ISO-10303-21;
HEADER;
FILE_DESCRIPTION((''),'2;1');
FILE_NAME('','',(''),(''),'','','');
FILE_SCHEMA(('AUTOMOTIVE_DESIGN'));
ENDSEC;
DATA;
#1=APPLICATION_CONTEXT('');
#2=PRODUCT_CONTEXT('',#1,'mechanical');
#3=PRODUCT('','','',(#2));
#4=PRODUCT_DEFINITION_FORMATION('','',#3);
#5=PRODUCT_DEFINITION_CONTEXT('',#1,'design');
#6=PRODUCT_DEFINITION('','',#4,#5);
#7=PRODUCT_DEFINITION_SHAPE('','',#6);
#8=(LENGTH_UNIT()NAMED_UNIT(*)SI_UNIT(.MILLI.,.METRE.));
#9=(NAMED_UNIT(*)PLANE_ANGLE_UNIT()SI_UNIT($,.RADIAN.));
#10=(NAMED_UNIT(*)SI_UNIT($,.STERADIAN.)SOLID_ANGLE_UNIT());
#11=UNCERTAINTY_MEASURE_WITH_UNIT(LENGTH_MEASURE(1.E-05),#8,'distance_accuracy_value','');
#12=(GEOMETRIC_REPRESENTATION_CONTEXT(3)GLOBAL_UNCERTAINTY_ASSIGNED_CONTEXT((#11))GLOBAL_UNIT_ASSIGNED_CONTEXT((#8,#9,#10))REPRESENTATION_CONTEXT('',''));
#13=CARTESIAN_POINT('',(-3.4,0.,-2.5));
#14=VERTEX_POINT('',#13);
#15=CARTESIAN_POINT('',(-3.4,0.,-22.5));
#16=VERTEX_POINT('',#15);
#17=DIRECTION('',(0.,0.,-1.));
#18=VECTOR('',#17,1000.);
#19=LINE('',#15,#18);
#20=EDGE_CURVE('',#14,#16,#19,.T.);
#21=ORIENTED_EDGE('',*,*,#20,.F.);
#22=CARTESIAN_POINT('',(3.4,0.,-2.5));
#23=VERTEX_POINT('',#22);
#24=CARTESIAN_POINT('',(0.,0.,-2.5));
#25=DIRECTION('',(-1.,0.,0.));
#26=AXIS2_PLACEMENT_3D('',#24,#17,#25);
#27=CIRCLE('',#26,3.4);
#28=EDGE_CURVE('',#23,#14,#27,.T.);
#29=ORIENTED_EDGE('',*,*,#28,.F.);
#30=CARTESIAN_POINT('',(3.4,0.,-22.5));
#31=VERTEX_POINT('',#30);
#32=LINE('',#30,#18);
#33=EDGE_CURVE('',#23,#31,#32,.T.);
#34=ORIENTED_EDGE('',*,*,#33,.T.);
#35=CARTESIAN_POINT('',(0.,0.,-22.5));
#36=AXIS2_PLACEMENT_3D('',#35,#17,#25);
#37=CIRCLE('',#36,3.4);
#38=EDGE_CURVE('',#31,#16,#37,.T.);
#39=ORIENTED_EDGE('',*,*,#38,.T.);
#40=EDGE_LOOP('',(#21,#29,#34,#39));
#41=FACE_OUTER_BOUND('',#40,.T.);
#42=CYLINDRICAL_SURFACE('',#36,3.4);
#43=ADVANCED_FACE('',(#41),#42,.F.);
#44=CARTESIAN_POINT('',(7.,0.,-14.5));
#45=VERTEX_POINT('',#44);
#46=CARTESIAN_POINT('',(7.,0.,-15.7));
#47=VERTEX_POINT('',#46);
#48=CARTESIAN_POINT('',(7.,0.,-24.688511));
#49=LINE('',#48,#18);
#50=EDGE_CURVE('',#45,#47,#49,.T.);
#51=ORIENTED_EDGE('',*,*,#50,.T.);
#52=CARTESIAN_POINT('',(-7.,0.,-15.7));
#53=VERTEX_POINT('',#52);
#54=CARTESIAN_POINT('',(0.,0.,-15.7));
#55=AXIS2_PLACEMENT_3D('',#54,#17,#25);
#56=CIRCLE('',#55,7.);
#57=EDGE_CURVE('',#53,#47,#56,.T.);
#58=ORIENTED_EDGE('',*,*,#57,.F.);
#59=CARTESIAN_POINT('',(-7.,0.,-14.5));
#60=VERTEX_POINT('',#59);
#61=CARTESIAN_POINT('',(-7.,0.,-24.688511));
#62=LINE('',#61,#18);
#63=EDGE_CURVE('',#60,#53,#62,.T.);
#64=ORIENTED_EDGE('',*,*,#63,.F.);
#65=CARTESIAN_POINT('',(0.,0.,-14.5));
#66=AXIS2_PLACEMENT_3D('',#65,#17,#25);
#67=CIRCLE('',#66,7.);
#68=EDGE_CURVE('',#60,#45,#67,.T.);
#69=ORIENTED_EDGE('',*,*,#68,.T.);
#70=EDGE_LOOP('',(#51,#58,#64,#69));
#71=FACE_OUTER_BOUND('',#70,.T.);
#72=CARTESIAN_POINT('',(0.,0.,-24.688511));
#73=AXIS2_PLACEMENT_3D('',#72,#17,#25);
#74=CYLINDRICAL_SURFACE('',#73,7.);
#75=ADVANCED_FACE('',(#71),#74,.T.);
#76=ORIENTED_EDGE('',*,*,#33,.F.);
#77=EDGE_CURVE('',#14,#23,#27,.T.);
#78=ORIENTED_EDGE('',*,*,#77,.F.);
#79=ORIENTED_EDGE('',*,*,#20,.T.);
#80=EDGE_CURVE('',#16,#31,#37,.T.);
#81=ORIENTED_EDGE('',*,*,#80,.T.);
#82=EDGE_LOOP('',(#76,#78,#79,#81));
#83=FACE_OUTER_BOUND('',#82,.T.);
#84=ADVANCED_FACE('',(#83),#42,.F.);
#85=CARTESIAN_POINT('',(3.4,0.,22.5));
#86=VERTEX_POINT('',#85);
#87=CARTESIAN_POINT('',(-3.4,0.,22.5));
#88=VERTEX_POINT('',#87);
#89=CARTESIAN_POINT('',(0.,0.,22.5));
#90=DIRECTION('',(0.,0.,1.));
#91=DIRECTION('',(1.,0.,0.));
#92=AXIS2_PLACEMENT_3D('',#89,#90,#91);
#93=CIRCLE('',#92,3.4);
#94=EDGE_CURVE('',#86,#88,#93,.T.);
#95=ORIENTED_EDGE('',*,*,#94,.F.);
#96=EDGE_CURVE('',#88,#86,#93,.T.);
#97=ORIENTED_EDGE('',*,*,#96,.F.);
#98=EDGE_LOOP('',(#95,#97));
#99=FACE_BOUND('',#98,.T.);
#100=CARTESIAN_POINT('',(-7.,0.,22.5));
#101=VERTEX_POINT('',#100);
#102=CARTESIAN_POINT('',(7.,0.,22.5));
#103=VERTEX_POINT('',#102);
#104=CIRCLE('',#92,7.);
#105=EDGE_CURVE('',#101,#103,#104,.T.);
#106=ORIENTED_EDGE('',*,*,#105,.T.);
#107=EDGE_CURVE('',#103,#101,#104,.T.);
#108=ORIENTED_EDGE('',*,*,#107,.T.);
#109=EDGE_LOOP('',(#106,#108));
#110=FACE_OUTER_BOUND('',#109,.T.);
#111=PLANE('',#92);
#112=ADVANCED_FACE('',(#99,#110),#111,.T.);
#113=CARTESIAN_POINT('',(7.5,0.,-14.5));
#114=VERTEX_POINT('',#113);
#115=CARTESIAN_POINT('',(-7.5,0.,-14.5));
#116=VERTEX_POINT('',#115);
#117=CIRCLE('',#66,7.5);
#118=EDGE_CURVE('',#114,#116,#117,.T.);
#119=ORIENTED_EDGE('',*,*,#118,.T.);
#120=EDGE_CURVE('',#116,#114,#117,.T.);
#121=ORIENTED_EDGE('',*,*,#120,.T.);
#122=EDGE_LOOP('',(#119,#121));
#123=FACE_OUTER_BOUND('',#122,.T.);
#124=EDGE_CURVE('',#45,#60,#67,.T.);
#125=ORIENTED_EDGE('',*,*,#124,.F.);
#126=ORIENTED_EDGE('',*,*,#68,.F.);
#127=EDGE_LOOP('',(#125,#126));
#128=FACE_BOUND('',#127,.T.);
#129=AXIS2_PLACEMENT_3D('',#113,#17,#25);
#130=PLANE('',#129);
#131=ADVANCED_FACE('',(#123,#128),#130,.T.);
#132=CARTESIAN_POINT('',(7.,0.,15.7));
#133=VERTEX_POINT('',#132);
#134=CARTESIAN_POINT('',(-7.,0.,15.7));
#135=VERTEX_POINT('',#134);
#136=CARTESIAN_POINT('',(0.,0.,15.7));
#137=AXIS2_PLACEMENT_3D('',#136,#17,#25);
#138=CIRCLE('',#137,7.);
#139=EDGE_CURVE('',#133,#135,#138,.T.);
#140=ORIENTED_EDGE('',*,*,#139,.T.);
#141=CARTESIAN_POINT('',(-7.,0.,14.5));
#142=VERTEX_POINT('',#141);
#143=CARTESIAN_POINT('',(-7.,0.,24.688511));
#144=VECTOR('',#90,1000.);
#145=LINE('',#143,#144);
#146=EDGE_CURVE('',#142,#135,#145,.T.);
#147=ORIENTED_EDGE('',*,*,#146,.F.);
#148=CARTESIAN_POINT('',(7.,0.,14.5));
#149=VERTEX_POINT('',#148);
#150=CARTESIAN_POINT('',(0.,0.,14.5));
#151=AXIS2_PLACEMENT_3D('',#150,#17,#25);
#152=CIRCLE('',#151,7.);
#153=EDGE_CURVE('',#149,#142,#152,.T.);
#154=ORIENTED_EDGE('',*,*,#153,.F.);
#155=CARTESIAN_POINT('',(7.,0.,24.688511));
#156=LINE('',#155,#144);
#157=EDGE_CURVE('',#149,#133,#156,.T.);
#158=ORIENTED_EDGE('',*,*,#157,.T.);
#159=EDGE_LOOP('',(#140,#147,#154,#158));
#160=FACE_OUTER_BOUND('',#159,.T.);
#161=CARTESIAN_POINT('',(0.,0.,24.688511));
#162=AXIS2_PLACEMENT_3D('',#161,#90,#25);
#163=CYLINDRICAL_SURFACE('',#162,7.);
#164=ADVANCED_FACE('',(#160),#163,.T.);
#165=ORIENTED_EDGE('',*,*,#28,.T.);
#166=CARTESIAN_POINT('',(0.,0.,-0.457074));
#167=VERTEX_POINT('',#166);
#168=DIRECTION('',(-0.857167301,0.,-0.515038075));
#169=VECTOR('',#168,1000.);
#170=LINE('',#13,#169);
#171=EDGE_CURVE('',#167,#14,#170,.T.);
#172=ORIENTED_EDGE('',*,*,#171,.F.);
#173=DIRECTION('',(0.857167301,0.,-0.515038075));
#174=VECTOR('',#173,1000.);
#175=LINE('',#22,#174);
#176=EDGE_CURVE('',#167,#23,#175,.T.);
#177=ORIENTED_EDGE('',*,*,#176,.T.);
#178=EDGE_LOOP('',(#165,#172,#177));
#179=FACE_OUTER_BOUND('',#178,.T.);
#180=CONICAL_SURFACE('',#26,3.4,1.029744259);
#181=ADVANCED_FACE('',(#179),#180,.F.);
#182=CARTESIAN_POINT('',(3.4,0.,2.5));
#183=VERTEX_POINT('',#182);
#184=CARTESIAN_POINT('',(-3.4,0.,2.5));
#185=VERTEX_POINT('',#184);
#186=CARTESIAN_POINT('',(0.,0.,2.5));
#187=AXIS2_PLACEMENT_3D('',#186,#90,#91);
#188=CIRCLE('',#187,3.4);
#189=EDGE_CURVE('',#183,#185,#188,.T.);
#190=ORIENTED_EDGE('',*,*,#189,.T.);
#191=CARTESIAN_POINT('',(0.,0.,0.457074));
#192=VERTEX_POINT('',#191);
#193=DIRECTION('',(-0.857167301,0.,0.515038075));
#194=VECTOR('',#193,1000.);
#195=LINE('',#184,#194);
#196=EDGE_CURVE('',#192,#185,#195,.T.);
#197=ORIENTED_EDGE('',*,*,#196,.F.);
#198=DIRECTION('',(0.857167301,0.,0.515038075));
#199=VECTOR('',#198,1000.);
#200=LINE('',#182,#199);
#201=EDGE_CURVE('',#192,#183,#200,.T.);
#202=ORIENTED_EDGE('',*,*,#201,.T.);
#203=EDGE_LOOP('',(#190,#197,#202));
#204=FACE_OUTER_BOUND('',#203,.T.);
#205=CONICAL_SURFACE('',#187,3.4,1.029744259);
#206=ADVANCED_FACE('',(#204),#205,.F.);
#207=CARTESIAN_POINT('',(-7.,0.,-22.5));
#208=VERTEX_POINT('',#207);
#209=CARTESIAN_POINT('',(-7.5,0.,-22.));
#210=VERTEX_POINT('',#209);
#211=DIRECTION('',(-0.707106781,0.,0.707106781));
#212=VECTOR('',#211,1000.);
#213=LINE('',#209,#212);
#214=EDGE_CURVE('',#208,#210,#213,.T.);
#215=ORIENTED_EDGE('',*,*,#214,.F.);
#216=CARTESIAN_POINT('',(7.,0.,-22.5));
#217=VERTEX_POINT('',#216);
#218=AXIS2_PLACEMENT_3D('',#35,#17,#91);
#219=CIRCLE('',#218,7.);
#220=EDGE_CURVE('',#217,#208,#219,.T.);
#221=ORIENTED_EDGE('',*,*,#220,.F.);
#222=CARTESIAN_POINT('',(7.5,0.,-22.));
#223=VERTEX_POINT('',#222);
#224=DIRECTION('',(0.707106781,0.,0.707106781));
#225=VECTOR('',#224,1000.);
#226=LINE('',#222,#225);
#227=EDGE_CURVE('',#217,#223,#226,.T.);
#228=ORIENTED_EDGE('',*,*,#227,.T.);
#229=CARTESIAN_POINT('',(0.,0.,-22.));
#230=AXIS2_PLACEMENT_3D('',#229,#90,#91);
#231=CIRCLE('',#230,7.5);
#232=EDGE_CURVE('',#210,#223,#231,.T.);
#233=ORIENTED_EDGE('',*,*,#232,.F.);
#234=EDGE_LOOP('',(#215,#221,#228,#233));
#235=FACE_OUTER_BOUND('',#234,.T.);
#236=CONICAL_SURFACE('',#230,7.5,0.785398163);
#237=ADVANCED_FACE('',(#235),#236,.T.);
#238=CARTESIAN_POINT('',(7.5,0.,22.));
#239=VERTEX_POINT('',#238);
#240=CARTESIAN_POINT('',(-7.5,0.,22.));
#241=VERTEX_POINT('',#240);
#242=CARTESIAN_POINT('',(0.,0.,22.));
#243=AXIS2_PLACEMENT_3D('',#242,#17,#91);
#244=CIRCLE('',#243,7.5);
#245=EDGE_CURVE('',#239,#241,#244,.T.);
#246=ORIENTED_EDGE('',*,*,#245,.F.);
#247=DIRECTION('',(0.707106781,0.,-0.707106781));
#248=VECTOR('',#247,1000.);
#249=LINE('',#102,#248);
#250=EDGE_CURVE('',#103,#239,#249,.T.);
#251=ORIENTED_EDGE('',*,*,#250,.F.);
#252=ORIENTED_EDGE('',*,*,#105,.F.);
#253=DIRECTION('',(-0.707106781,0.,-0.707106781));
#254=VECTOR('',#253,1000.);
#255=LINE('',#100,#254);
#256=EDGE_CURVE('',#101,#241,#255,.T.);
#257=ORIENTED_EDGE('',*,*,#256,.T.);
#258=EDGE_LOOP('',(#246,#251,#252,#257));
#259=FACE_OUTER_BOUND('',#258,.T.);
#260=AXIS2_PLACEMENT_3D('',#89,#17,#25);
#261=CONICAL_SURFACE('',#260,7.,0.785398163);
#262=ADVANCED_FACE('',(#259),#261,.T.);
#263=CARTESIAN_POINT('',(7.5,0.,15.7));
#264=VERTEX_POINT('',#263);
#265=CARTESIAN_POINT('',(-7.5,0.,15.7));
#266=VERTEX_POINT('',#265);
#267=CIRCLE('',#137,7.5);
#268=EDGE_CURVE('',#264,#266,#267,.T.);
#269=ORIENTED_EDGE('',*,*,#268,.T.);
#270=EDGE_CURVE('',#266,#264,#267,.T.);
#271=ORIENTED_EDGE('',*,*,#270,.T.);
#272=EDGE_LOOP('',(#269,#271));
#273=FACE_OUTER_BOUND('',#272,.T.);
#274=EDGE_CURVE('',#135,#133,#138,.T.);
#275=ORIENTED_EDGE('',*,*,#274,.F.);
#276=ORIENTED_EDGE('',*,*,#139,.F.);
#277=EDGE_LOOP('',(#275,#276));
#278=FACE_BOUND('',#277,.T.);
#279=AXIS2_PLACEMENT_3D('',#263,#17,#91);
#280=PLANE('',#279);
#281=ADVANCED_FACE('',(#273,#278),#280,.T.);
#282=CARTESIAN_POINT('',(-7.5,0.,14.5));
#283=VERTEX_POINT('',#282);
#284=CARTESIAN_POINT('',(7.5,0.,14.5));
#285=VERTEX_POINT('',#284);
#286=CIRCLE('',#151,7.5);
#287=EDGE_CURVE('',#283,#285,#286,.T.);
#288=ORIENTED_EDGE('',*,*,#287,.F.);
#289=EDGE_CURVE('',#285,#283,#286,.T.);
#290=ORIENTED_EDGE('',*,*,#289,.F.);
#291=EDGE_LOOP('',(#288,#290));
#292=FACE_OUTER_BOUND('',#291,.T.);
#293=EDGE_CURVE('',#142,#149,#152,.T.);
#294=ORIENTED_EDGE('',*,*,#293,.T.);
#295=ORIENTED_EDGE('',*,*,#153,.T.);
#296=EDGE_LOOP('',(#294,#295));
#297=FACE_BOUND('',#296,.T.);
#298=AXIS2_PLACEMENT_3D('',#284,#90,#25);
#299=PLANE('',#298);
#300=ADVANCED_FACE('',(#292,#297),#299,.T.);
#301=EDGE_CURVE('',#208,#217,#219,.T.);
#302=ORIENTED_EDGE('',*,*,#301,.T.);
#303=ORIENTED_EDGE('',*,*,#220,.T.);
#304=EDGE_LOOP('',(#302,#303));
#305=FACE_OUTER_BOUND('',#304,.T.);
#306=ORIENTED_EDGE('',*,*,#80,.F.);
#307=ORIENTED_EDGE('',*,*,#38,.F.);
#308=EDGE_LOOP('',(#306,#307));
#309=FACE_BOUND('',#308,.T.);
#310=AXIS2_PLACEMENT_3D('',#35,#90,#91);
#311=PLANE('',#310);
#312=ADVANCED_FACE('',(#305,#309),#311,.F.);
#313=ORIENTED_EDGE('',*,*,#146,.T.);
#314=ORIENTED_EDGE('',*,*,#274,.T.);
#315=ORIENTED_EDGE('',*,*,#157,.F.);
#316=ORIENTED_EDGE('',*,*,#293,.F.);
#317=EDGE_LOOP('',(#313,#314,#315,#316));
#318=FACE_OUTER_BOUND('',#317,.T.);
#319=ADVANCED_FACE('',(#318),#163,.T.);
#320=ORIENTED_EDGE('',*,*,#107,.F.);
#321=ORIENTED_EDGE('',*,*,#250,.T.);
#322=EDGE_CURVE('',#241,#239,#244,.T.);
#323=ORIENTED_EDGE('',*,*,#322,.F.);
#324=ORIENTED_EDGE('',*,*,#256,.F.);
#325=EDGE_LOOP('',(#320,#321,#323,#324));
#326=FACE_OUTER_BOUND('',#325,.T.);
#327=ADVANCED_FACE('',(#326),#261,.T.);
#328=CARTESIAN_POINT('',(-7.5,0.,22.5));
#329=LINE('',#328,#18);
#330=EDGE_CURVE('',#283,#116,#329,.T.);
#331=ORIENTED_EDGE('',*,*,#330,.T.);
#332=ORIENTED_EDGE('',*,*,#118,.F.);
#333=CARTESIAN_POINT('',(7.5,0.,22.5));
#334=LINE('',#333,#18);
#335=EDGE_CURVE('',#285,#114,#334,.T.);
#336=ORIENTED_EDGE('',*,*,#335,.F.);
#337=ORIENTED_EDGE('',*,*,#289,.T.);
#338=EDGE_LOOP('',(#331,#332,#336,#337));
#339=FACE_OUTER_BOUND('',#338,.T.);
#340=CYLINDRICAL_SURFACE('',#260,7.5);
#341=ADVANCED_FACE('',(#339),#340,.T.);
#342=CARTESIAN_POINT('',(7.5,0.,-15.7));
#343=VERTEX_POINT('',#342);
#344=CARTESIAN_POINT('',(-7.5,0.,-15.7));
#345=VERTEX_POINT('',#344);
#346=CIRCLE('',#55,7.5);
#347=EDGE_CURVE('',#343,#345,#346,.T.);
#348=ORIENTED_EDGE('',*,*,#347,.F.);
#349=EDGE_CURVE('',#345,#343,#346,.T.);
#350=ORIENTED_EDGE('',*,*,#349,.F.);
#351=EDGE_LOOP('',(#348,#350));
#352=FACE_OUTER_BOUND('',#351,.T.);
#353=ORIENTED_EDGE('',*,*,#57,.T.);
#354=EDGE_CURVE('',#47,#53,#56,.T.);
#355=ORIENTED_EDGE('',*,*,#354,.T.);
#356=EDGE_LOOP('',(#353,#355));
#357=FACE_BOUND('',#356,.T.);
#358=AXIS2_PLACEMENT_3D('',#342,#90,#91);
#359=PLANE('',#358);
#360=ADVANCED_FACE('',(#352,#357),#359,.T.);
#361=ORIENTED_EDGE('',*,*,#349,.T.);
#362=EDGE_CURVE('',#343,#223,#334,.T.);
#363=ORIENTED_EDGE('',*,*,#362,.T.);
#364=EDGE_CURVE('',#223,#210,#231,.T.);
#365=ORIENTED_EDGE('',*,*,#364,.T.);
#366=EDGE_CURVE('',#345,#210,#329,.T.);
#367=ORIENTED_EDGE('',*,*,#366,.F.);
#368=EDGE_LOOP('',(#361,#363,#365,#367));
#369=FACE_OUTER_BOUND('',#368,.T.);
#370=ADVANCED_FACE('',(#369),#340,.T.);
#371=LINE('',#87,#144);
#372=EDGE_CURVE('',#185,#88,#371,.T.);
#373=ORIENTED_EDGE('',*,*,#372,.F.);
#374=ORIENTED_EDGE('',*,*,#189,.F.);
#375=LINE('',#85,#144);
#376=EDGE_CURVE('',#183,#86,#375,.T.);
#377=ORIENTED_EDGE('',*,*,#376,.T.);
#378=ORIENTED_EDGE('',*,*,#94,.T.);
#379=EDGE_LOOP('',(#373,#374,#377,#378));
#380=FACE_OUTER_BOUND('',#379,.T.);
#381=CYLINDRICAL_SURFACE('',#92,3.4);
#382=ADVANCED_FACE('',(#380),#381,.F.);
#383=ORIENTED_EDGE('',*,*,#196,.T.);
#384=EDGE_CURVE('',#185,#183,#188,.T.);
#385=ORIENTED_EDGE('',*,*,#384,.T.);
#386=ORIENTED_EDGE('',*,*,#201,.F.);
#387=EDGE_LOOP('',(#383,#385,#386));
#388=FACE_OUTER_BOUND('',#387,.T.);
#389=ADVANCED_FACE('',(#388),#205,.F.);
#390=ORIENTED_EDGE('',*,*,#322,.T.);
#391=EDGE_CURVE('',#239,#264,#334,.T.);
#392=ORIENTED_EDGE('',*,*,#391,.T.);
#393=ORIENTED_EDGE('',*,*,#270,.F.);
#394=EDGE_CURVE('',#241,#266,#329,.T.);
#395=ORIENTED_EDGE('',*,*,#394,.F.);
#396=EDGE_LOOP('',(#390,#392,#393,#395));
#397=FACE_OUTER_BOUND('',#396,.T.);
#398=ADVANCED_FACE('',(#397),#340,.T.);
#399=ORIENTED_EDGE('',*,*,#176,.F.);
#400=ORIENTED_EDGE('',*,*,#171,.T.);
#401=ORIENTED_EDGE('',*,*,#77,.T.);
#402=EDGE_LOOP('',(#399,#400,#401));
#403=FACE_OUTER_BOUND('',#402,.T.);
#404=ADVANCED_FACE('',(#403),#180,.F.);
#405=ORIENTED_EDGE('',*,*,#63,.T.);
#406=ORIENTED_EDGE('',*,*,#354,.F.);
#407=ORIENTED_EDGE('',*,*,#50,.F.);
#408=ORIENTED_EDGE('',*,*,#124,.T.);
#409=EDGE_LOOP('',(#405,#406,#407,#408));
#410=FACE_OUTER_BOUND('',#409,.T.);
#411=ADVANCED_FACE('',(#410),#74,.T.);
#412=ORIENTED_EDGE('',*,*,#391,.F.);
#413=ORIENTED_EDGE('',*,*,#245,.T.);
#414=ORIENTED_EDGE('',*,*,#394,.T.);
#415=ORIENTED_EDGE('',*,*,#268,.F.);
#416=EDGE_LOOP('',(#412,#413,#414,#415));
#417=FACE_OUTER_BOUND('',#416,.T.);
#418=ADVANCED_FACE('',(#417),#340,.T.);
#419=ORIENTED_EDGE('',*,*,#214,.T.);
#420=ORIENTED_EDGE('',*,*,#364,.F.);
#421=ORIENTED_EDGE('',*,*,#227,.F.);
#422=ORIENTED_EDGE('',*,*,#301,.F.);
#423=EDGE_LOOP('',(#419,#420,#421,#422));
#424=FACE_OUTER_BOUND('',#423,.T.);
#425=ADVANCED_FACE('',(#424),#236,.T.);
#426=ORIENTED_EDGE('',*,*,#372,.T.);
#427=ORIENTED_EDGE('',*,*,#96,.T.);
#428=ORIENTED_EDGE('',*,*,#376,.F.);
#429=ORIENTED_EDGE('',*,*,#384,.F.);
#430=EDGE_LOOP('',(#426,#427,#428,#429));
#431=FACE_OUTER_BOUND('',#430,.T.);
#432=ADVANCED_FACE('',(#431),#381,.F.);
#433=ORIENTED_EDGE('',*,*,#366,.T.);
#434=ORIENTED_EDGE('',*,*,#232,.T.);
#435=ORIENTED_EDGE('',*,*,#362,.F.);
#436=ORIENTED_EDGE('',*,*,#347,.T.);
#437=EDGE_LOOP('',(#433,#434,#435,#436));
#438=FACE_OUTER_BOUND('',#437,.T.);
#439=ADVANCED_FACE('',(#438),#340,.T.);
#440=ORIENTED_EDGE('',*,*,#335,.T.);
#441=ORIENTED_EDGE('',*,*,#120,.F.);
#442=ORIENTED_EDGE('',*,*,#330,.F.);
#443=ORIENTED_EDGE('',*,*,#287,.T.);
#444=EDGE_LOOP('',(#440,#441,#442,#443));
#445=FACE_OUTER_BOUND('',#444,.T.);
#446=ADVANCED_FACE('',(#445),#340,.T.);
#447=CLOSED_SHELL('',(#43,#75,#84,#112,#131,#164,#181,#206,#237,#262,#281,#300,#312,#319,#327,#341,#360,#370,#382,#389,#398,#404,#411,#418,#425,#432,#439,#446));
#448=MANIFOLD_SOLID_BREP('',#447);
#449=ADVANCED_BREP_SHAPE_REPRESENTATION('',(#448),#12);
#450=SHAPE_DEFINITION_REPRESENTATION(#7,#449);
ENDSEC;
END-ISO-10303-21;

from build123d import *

# Parameters (mm, degrees)
SKETCH_1_R      = 7.5
EXTRUDE_1_DEPTH = 22.5
CHAMFER_1_SIZE  = 0.5
SKETCH_4_W      = 0.5
SKETCH_4_H      = 1.2


with BuildPart() as part:
    # 草图1 → 凸台-拉伸1 (new, symmetric)
    with BuildSketch(Plane.XY):
        with Locations(Location((0, 0, 0), (0, 0, 180))):
            Circle(SKETCH_1_R)
    extrude(amount=EXTRUDE_1_DEPTH, both=True)

    # 草图2 → M8 螺纹孔1 (revolve, cut)
    with BuildSketch(Plane(origin=(0, 0, 22.5), x_dir=(0, -1, 0), z_dir=(1, 0, 0))):
        Polygon((0, 0), (0, 22.042926105), (3.4, 20), (3.4, 0), align=None)
    hole_wizard_m8_1 = revolve(axis=Axis((0, 0, 28.85), (0, 0, -1)), mode=Mode.SUBTRACT)

    # 倒角1
    chamfer_1_edges = [part.edges().sort_by_distance(p)[0] for p in [
        (7.5, 0, -22.5),
        (7.5, 0, 22.5),
    ]]
    chamfer(chamfer_1_edges, length=CHAMFER_1_SIZE)

    # 镜向3: M8 螺纹孔1 across plane
    add(hole_wizard_m8_1.mirror(Plane.XY), mode=Mode.SUBTRACT)

    # 草图4 → 切除-旋转1 (revolve, cut)
    with BuildSketch(Plane(origin=(0, 0, 0), x_dir=(1, 0, 0), z_dir=(0, 1, 0)), mode=Mode.PRIVATE) as cut_revolve_1_sk:
        with Locations((7.25, 15.1)):
            Rectangle(SKETCH_4_W, SKETCH_4_H)
    cut_revolve_1 = revolve(cut_revolve_1_sk.sketch.rotate(Axis((0, 0, -24.688510649), (0, 0, 1)), 180), axis=Axis((0, 0, -24.688510649), (0, 0, 1)), mode=Mode.SUBTRACT)

    # 镜向5: 切除-旋转1 across plane
    add(cut_revolve_1.mirror(Plane.XY), mode=Mode.SUBTRACT)


solid = part.part
